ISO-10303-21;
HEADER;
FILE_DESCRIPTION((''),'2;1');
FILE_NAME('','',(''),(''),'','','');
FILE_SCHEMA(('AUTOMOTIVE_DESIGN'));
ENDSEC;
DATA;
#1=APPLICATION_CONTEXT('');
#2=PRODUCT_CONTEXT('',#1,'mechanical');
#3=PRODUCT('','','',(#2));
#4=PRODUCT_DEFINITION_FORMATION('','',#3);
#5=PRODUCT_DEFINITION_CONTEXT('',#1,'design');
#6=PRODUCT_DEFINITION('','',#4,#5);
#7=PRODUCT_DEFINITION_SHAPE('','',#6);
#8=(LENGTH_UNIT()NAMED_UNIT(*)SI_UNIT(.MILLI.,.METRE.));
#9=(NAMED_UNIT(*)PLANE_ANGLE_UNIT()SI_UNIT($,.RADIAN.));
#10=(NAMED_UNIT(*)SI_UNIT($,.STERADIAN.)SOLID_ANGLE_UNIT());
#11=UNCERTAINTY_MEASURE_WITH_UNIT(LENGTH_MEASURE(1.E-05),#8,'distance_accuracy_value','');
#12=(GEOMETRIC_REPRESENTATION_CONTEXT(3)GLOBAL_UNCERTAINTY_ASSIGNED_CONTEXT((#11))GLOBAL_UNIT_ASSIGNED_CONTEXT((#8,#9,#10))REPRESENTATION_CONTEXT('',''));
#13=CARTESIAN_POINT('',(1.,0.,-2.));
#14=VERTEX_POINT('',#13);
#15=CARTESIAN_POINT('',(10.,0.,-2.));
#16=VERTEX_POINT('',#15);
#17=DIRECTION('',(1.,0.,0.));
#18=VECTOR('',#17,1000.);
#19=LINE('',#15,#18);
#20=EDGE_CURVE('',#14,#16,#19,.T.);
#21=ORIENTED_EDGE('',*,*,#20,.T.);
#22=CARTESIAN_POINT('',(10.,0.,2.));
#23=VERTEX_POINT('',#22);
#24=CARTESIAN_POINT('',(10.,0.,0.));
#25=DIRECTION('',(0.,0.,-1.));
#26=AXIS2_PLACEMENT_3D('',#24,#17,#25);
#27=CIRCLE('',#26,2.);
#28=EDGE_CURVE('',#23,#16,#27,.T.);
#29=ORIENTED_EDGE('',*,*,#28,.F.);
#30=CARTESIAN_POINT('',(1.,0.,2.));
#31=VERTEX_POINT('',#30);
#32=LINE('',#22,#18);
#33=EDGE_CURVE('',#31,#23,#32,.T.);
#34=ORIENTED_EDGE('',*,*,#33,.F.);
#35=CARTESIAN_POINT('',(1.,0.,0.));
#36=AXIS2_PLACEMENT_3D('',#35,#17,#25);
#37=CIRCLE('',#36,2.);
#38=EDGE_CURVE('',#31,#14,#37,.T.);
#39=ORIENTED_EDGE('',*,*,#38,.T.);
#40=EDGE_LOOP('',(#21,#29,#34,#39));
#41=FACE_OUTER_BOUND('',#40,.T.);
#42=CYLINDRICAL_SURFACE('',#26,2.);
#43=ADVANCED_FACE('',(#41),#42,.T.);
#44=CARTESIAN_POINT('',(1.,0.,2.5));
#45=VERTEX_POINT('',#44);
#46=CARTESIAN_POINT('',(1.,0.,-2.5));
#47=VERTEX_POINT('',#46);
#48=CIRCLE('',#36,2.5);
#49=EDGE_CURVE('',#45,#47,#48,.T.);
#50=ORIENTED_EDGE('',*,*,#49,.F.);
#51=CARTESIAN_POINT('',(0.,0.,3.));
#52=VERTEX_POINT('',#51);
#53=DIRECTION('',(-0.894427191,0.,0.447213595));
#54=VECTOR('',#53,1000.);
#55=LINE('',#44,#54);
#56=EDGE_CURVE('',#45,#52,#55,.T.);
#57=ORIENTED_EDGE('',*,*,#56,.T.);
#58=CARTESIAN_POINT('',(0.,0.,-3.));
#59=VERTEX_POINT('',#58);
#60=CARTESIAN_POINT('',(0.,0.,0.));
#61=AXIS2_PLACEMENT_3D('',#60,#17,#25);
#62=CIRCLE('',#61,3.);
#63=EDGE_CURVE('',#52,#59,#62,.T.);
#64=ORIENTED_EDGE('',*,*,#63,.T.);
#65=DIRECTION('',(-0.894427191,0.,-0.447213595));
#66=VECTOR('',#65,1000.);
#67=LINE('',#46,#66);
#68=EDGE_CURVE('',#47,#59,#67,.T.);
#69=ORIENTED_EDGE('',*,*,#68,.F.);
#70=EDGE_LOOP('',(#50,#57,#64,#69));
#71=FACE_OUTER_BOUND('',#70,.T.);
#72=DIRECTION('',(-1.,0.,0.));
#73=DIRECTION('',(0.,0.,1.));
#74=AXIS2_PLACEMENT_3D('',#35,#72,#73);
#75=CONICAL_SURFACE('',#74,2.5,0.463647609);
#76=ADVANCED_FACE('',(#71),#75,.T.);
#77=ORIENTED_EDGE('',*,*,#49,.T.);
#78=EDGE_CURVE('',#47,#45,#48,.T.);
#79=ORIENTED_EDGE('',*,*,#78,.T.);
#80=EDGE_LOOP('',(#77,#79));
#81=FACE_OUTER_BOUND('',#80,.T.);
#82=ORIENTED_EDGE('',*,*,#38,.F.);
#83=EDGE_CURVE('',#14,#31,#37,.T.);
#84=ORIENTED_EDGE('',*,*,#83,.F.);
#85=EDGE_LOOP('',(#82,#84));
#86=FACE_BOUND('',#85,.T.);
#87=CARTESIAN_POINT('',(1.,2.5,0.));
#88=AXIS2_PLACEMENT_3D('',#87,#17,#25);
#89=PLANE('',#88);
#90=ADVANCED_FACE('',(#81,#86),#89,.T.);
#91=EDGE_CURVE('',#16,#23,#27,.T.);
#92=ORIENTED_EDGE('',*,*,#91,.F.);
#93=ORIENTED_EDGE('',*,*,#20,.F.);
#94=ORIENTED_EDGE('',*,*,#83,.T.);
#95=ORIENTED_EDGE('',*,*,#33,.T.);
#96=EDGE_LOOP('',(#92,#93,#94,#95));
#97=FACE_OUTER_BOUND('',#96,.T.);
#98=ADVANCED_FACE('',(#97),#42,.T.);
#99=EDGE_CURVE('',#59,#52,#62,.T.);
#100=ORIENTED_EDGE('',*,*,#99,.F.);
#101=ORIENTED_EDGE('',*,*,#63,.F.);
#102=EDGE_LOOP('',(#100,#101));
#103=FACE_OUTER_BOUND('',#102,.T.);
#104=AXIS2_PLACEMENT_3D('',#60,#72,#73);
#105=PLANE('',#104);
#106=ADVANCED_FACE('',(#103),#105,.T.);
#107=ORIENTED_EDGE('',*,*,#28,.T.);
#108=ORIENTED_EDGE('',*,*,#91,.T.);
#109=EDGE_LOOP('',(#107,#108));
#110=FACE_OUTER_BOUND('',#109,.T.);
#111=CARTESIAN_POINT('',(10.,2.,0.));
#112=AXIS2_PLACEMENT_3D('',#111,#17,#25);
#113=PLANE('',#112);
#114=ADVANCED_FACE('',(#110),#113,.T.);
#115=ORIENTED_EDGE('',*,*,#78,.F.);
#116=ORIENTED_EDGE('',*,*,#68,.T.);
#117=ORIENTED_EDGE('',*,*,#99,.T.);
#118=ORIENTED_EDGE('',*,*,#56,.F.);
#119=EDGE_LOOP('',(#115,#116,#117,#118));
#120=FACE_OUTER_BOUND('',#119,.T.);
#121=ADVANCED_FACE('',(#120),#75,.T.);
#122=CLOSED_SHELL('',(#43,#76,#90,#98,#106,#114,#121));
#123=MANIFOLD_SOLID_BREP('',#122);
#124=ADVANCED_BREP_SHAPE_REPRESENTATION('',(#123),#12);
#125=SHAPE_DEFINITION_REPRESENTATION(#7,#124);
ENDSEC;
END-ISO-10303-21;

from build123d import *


with BuildPart() as part:
    # Sketch1 → Revolve1 (revolve)
    with BuildSketch(Plane.XY, mode=Mode.PRIVATE) as revolve1_sk:
        Polygon((0, 0), (0, 3), (1, 2.5), (1, 2), (10, 2), (10, 0), align=None)
    revolve(revolve1_sk.sketch.rotate(Axis((10, 0, 0), (-1, 0, 0)), 90), axis=Axis((10, 0, 0), (-1, 0, 0)))


solid = part.part
